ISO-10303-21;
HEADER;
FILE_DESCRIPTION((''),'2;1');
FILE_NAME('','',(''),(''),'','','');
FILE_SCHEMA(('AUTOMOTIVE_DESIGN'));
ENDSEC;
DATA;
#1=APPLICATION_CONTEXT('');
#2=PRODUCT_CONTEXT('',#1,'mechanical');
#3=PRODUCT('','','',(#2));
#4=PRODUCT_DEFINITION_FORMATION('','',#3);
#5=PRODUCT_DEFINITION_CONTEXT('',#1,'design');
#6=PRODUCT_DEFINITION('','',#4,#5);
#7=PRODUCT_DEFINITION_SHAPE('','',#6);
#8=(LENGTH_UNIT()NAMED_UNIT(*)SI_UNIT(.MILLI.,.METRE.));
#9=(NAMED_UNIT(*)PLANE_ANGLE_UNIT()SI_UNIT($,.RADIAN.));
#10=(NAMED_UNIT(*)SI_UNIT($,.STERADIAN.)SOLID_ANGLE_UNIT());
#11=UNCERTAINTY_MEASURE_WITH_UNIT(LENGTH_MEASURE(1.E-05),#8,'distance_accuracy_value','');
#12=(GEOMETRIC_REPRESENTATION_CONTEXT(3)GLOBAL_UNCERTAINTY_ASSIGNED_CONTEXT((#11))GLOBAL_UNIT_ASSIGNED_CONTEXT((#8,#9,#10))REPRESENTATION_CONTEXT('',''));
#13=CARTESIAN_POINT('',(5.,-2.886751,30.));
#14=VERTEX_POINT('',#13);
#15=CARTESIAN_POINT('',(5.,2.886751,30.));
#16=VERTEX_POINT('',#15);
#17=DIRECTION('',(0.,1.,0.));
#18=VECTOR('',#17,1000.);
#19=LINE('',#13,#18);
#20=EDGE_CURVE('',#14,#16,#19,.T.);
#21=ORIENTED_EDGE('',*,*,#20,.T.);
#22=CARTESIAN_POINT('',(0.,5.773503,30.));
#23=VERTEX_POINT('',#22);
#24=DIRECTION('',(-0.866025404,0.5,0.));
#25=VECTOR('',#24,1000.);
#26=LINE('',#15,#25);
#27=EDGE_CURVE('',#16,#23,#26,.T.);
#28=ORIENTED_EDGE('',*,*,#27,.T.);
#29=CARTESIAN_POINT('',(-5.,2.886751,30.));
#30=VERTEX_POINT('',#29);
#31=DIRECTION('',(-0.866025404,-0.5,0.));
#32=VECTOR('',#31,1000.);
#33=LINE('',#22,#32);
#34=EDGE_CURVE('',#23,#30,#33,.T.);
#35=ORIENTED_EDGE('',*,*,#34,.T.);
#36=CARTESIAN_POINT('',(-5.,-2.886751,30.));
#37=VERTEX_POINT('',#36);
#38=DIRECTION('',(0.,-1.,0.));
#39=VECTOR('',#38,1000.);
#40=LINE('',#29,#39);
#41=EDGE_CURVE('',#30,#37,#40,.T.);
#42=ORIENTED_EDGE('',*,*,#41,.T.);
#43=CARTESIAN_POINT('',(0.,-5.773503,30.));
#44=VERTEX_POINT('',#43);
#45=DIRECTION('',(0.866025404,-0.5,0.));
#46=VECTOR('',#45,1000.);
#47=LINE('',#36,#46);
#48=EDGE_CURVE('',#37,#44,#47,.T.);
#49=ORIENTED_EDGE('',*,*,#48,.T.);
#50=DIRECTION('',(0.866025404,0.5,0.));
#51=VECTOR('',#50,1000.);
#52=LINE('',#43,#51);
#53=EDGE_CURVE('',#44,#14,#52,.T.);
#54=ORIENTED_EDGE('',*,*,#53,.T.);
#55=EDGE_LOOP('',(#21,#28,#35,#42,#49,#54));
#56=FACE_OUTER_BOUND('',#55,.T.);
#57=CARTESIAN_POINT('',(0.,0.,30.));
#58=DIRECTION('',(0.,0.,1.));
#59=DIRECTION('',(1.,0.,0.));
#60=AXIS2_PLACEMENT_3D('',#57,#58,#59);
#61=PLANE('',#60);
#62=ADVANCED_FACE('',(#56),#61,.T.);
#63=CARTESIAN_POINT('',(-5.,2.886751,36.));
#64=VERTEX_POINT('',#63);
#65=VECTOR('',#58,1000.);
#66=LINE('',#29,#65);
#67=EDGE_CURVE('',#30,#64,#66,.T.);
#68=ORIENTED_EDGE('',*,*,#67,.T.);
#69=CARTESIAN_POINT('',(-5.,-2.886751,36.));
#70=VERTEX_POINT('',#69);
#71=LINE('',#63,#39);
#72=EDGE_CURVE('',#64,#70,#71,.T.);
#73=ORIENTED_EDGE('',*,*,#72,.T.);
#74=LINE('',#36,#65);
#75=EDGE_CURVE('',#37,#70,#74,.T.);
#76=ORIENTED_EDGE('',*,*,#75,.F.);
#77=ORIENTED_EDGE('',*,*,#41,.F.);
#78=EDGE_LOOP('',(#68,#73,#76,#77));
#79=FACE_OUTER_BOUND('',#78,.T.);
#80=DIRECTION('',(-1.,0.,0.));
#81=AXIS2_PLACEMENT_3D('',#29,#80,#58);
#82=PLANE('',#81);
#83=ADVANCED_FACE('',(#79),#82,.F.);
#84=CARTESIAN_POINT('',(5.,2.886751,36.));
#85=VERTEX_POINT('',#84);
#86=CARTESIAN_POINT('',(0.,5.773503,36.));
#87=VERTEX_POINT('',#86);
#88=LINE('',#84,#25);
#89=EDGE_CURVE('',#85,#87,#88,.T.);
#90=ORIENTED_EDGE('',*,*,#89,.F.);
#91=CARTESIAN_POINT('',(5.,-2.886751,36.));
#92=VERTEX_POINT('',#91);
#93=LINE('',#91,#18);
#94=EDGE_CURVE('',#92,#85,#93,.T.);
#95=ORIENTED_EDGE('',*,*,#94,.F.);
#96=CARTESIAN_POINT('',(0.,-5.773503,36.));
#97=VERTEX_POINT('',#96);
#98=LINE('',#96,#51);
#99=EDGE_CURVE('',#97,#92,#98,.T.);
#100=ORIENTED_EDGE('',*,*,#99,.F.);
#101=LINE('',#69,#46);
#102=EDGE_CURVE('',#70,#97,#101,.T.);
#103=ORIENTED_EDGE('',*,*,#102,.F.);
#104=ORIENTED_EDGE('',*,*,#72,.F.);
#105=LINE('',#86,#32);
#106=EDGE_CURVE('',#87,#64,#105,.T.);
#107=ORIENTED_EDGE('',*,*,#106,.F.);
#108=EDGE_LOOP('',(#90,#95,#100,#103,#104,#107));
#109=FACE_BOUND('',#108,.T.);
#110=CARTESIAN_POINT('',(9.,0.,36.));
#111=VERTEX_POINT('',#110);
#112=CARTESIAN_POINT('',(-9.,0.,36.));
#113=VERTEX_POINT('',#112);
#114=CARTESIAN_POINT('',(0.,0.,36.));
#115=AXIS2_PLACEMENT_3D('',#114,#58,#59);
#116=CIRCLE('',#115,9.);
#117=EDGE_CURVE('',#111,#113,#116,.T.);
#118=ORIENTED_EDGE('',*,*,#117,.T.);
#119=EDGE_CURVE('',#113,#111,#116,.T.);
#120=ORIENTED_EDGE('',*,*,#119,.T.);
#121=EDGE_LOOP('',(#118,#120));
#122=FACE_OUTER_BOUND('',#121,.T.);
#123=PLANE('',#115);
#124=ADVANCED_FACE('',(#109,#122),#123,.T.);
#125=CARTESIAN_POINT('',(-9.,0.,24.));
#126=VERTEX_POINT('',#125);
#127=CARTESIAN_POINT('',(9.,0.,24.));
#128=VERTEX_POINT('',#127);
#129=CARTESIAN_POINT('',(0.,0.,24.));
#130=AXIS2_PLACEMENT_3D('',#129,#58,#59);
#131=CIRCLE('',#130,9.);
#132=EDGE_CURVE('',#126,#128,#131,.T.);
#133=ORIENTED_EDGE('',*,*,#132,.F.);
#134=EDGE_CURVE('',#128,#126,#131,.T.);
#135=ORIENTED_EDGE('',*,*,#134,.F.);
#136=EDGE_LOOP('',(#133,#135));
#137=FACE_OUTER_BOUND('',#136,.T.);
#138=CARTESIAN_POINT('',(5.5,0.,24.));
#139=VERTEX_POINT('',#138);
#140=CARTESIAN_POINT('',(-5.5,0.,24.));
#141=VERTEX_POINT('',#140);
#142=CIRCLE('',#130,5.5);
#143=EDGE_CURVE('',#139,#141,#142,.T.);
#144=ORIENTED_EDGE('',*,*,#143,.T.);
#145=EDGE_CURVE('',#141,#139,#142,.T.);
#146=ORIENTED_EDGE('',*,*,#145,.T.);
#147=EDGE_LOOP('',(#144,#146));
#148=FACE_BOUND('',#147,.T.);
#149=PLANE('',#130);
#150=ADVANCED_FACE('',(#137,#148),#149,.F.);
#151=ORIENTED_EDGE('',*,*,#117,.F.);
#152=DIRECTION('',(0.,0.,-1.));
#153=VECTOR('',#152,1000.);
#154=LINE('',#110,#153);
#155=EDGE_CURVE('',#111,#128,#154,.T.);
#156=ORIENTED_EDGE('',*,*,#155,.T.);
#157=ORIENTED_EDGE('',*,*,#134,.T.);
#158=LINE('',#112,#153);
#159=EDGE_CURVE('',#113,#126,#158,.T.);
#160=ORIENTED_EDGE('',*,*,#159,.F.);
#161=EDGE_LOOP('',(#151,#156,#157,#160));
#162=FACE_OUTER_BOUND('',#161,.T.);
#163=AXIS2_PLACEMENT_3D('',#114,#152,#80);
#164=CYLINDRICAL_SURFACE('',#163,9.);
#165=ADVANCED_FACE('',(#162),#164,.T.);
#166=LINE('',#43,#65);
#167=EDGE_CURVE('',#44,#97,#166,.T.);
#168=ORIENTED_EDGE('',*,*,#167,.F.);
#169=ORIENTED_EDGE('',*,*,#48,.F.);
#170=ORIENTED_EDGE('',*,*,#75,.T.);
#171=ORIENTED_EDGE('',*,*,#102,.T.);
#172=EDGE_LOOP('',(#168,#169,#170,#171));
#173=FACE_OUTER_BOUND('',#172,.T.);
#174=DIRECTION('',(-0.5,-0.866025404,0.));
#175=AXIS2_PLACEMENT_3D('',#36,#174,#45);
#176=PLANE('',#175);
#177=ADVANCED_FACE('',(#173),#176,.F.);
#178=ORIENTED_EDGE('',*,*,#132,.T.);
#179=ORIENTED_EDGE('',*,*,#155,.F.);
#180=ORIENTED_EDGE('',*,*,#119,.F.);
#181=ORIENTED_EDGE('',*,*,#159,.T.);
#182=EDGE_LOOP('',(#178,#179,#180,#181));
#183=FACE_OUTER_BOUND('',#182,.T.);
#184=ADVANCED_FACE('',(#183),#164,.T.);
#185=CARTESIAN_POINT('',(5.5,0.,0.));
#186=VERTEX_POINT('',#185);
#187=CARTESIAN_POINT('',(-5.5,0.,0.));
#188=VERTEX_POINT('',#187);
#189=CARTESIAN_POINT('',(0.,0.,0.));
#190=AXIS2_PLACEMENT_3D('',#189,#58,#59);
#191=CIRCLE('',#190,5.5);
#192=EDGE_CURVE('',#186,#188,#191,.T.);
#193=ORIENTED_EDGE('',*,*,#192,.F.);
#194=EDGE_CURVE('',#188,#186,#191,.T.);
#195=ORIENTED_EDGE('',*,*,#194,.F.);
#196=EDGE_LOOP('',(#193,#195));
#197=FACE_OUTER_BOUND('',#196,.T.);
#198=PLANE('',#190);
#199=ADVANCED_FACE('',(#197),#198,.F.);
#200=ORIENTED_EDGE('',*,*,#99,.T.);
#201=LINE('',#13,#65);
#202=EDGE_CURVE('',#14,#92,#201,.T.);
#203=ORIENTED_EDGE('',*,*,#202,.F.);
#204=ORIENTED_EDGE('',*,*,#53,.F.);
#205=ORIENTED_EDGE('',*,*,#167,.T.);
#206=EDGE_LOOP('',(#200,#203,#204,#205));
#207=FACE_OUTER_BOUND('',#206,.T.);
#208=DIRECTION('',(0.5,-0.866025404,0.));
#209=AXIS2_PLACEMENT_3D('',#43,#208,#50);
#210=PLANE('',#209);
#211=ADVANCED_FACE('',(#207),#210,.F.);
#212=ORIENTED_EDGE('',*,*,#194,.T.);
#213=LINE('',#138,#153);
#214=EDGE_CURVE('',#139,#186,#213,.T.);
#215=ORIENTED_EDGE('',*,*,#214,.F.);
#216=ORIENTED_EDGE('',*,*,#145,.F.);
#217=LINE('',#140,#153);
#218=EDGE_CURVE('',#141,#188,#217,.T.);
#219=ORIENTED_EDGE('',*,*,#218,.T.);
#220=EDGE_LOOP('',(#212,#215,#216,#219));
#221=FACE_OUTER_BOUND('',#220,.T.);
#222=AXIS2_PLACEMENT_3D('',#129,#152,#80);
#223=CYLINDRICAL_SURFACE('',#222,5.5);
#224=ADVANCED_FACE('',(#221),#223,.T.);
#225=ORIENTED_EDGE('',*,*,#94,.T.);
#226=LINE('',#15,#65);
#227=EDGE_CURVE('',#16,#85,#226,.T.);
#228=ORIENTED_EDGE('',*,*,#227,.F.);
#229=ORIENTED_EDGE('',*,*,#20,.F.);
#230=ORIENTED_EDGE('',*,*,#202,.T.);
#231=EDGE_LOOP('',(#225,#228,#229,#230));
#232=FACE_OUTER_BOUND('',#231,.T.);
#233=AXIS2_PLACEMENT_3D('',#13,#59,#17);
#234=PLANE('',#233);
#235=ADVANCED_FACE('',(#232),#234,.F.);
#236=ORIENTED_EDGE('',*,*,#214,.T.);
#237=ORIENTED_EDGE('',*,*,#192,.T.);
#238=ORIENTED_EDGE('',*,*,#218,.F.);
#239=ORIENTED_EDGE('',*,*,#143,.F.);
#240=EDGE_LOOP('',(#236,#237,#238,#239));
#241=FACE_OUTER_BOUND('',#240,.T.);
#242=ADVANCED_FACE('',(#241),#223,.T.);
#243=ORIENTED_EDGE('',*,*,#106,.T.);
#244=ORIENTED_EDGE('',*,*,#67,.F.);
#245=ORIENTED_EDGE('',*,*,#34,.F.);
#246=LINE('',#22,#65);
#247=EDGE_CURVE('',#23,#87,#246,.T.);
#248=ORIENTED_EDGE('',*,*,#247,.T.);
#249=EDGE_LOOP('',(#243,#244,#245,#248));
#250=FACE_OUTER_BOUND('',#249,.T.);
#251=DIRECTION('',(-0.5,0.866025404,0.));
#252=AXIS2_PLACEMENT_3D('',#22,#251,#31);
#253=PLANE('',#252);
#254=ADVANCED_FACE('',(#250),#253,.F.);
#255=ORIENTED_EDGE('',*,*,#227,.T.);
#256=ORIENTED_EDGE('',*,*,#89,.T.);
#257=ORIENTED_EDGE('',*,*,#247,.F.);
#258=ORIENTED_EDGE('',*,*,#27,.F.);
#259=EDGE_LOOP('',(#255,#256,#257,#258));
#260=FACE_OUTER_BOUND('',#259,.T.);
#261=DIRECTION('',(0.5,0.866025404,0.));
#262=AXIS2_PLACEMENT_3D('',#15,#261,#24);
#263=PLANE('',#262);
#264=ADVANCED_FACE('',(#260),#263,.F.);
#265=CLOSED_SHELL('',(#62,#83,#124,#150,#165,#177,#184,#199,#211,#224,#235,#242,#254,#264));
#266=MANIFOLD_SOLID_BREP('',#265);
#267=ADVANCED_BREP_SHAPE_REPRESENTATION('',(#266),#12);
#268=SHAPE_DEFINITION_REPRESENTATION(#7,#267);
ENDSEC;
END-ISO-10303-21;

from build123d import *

# Parameters (mm, degrees)
SKETCH1_R           = 5.5
BOSS_EXTRUDE1_DEPTH = 24
SKETCH2_R           = 9
BOSS_EXTRUDE2_DEPTH = 12
CUT_EXTRUDE1_DEPTH  = 6


with BuildPart() as part:
    # Sketch1 → Boss-Extrude1 (new body)
    with BuildSketch(Plane.XY):
        Circle(SKETCH1_R)
    extrude(amount=BOSS_EXTRUDE1_DEPTH)

    # Sketch2 → Boss-Extrude2 (add)
    with BuildSketch(Plane.XY.offset(24)):
        Circle(SKETCH2_R)
    extrude(amount=BOSS_EXTRUDE2_DEPTH)

    # Sketch3 → Cut-Extrude1 (cut)
    with BuildSketch(Plane.XY.offset(36)):
        Polygon((0, 5.773502692), (-5, 2.886751346), (-5, -2.886751346), (0, -5.773502692), (5, -2.886751346), (5, 2.886751346), align=None)
    extrude(amount=-CUT_EXTRUDE1_DEPTH, mode=Mode.SUBTRACT)


solid = part.part
